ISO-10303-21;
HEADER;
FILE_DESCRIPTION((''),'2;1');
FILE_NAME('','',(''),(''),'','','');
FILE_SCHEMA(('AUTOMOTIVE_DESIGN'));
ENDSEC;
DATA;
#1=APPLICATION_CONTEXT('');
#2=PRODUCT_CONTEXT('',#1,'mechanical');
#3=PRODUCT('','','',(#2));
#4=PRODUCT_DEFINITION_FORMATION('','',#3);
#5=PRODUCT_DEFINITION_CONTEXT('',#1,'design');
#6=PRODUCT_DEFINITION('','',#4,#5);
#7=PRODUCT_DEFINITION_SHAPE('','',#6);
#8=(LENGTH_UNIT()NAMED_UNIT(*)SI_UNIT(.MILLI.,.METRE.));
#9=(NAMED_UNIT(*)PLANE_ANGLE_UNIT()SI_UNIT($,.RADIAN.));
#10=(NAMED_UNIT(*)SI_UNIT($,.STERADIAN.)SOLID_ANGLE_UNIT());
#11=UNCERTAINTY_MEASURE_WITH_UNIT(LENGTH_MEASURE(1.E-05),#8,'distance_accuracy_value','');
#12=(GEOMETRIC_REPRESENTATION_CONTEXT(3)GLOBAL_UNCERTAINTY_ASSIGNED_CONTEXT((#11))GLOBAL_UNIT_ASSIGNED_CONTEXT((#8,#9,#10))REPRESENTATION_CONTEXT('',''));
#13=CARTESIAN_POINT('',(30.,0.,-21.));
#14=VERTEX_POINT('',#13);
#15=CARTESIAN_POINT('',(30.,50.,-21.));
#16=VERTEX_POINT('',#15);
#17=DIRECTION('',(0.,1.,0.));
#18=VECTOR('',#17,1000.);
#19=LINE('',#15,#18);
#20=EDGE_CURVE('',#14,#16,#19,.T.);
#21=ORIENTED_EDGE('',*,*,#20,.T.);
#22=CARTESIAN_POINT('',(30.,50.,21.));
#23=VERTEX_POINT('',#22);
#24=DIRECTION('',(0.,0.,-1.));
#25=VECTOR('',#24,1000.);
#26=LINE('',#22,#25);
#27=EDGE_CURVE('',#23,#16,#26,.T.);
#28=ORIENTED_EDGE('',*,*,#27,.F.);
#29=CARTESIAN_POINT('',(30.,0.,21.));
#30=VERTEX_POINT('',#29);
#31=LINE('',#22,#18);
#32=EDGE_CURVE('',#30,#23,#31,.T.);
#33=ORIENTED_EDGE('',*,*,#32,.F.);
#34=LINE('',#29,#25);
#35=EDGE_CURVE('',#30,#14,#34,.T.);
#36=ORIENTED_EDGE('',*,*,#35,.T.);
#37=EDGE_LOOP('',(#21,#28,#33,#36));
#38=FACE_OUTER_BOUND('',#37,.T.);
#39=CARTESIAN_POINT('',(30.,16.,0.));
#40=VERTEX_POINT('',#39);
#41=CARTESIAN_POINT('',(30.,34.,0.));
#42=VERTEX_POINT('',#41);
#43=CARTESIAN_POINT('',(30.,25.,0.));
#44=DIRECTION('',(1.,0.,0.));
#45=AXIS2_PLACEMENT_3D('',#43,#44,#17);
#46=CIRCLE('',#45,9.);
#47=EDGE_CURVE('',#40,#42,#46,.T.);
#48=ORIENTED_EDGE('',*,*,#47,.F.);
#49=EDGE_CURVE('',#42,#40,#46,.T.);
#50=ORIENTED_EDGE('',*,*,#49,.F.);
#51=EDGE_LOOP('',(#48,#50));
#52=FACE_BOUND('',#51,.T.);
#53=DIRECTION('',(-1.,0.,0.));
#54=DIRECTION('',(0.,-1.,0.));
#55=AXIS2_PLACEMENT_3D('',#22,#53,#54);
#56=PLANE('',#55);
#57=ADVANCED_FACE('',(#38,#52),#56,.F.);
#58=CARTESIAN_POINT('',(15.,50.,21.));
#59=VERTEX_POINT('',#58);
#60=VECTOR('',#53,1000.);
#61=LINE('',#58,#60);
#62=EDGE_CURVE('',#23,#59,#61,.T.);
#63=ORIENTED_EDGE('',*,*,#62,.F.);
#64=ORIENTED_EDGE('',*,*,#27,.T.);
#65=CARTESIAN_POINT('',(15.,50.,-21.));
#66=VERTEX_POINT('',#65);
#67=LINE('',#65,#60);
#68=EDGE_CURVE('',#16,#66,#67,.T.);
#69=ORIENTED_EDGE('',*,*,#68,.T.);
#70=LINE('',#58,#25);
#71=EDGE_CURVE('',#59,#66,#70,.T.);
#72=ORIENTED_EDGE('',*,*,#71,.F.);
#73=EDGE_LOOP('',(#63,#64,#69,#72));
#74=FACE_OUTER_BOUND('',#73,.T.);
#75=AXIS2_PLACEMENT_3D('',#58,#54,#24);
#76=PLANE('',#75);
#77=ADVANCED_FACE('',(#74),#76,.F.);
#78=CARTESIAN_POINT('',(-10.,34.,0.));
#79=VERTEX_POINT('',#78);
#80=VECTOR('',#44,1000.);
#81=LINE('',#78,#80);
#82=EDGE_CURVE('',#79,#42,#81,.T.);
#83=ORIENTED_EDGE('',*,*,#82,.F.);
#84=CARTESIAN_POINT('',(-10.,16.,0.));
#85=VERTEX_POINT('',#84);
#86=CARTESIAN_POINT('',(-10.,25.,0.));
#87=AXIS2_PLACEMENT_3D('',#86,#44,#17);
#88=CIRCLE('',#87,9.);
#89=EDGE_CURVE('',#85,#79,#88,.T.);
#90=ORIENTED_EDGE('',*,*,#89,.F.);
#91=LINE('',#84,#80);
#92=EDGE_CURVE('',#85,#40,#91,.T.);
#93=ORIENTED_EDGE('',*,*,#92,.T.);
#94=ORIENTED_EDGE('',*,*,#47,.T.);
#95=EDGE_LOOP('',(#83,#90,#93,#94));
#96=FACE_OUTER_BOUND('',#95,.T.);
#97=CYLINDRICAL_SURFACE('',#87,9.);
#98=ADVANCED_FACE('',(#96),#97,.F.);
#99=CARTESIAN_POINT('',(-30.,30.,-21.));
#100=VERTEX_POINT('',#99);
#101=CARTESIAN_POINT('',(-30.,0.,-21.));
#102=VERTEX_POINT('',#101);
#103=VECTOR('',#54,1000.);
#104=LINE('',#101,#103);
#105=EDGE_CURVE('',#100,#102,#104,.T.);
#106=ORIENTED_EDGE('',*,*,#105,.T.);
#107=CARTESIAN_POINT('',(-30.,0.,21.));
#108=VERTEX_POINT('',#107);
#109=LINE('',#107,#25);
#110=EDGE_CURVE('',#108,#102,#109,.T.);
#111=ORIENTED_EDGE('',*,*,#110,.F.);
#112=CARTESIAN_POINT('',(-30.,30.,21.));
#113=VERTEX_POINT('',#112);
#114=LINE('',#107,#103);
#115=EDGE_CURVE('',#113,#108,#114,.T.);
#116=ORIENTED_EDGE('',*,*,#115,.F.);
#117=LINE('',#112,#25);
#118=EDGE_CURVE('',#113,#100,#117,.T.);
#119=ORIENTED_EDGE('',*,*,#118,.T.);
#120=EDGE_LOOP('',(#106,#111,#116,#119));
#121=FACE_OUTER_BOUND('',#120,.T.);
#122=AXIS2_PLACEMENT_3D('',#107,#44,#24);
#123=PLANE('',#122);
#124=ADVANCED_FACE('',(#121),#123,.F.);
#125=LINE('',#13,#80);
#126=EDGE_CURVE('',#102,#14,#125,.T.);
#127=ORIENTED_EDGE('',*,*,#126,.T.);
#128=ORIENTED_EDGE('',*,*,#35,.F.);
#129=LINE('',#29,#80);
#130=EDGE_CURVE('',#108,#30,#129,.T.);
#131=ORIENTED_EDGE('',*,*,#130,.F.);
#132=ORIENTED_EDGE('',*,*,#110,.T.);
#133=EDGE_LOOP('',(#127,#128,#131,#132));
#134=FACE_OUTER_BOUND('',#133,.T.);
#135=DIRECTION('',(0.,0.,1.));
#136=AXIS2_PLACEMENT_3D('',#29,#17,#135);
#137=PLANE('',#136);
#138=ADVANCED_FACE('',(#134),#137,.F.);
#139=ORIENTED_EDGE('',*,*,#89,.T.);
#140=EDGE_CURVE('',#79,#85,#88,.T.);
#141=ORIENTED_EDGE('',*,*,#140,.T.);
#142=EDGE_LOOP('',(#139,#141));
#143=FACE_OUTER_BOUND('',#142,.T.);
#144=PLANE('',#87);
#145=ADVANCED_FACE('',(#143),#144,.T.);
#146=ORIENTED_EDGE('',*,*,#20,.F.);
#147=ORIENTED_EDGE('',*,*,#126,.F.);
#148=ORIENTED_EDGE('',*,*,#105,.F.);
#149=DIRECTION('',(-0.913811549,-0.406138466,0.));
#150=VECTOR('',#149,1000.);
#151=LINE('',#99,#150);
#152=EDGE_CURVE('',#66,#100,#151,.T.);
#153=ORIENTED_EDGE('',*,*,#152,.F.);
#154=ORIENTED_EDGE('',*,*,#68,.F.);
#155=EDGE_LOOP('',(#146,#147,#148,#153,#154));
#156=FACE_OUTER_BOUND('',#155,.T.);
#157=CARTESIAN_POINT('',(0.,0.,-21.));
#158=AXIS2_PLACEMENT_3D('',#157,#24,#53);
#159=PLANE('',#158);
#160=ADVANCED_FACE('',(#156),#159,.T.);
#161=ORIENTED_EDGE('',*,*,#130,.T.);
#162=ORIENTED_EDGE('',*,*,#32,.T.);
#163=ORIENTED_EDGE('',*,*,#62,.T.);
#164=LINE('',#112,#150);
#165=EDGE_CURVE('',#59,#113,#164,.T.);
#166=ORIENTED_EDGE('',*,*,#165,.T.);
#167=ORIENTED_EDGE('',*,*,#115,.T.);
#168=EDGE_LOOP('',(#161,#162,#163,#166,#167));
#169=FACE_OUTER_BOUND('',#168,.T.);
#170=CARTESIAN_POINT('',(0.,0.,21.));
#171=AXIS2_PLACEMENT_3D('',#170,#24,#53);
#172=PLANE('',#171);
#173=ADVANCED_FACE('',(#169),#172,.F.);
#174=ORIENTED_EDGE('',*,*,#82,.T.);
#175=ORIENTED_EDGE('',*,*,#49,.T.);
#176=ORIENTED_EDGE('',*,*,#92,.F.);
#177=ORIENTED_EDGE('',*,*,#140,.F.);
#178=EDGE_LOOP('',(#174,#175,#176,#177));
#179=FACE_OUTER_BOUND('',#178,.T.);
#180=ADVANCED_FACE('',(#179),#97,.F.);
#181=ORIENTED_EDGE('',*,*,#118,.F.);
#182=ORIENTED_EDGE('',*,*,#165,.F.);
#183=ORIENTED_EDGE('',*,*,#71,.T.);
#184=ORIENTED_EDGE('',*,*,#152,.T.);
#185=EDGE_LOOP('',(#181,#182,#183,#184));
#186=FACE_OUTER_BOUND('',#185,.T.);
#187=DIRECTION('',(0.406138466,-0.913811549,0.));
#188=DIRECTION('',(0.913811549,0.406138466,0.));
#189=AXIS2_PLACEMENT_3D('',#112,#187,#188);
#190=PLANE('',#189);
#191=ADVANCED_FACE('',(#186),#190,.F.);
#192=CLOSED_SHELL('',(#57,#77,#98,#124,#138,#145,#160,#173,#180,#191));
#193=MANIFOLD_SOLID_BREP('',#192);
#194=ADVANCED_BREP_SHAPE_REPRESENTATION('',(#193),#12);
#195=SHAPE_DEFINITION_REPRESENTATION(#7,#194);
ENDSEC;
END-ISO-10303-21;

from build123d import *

# Parameters (mm, degrees)
BLOCK_BODY_DEPTH        = 21
BORE_18_SKETCH_R        = 9
BORE_18_X_40_DEEP_DEPTH = 40


with BuildPart() as part:
    # Block Profile Sketch → Block Body (new, symmetric)
    with BuildSketch(Plane.XY):
        Polygon((30, 0), (-30, 0), (-30, 30), (15, 50), (30, 50), align=None)
    extrude(amount=BLOCK_BODY_DEPTH, both=True)

    # Bore Ø18 Sketch → Bore Ø18 x 40 Deep (cut)
    with BuildSketch(Plane(origin=(30, 0, 0), x_dir=(0, 0, -1), z_dir=(1, 0, 0))):
        with Locations(Location((0, 25, 0), (0, 0, 90))):
            Circle(BORE_18_SKETCH_R)
    extrude(amount=-BORE_18_X_40_DEEP_DEPTH, mode=Mode.SUBTRACT)


solid = part.part
